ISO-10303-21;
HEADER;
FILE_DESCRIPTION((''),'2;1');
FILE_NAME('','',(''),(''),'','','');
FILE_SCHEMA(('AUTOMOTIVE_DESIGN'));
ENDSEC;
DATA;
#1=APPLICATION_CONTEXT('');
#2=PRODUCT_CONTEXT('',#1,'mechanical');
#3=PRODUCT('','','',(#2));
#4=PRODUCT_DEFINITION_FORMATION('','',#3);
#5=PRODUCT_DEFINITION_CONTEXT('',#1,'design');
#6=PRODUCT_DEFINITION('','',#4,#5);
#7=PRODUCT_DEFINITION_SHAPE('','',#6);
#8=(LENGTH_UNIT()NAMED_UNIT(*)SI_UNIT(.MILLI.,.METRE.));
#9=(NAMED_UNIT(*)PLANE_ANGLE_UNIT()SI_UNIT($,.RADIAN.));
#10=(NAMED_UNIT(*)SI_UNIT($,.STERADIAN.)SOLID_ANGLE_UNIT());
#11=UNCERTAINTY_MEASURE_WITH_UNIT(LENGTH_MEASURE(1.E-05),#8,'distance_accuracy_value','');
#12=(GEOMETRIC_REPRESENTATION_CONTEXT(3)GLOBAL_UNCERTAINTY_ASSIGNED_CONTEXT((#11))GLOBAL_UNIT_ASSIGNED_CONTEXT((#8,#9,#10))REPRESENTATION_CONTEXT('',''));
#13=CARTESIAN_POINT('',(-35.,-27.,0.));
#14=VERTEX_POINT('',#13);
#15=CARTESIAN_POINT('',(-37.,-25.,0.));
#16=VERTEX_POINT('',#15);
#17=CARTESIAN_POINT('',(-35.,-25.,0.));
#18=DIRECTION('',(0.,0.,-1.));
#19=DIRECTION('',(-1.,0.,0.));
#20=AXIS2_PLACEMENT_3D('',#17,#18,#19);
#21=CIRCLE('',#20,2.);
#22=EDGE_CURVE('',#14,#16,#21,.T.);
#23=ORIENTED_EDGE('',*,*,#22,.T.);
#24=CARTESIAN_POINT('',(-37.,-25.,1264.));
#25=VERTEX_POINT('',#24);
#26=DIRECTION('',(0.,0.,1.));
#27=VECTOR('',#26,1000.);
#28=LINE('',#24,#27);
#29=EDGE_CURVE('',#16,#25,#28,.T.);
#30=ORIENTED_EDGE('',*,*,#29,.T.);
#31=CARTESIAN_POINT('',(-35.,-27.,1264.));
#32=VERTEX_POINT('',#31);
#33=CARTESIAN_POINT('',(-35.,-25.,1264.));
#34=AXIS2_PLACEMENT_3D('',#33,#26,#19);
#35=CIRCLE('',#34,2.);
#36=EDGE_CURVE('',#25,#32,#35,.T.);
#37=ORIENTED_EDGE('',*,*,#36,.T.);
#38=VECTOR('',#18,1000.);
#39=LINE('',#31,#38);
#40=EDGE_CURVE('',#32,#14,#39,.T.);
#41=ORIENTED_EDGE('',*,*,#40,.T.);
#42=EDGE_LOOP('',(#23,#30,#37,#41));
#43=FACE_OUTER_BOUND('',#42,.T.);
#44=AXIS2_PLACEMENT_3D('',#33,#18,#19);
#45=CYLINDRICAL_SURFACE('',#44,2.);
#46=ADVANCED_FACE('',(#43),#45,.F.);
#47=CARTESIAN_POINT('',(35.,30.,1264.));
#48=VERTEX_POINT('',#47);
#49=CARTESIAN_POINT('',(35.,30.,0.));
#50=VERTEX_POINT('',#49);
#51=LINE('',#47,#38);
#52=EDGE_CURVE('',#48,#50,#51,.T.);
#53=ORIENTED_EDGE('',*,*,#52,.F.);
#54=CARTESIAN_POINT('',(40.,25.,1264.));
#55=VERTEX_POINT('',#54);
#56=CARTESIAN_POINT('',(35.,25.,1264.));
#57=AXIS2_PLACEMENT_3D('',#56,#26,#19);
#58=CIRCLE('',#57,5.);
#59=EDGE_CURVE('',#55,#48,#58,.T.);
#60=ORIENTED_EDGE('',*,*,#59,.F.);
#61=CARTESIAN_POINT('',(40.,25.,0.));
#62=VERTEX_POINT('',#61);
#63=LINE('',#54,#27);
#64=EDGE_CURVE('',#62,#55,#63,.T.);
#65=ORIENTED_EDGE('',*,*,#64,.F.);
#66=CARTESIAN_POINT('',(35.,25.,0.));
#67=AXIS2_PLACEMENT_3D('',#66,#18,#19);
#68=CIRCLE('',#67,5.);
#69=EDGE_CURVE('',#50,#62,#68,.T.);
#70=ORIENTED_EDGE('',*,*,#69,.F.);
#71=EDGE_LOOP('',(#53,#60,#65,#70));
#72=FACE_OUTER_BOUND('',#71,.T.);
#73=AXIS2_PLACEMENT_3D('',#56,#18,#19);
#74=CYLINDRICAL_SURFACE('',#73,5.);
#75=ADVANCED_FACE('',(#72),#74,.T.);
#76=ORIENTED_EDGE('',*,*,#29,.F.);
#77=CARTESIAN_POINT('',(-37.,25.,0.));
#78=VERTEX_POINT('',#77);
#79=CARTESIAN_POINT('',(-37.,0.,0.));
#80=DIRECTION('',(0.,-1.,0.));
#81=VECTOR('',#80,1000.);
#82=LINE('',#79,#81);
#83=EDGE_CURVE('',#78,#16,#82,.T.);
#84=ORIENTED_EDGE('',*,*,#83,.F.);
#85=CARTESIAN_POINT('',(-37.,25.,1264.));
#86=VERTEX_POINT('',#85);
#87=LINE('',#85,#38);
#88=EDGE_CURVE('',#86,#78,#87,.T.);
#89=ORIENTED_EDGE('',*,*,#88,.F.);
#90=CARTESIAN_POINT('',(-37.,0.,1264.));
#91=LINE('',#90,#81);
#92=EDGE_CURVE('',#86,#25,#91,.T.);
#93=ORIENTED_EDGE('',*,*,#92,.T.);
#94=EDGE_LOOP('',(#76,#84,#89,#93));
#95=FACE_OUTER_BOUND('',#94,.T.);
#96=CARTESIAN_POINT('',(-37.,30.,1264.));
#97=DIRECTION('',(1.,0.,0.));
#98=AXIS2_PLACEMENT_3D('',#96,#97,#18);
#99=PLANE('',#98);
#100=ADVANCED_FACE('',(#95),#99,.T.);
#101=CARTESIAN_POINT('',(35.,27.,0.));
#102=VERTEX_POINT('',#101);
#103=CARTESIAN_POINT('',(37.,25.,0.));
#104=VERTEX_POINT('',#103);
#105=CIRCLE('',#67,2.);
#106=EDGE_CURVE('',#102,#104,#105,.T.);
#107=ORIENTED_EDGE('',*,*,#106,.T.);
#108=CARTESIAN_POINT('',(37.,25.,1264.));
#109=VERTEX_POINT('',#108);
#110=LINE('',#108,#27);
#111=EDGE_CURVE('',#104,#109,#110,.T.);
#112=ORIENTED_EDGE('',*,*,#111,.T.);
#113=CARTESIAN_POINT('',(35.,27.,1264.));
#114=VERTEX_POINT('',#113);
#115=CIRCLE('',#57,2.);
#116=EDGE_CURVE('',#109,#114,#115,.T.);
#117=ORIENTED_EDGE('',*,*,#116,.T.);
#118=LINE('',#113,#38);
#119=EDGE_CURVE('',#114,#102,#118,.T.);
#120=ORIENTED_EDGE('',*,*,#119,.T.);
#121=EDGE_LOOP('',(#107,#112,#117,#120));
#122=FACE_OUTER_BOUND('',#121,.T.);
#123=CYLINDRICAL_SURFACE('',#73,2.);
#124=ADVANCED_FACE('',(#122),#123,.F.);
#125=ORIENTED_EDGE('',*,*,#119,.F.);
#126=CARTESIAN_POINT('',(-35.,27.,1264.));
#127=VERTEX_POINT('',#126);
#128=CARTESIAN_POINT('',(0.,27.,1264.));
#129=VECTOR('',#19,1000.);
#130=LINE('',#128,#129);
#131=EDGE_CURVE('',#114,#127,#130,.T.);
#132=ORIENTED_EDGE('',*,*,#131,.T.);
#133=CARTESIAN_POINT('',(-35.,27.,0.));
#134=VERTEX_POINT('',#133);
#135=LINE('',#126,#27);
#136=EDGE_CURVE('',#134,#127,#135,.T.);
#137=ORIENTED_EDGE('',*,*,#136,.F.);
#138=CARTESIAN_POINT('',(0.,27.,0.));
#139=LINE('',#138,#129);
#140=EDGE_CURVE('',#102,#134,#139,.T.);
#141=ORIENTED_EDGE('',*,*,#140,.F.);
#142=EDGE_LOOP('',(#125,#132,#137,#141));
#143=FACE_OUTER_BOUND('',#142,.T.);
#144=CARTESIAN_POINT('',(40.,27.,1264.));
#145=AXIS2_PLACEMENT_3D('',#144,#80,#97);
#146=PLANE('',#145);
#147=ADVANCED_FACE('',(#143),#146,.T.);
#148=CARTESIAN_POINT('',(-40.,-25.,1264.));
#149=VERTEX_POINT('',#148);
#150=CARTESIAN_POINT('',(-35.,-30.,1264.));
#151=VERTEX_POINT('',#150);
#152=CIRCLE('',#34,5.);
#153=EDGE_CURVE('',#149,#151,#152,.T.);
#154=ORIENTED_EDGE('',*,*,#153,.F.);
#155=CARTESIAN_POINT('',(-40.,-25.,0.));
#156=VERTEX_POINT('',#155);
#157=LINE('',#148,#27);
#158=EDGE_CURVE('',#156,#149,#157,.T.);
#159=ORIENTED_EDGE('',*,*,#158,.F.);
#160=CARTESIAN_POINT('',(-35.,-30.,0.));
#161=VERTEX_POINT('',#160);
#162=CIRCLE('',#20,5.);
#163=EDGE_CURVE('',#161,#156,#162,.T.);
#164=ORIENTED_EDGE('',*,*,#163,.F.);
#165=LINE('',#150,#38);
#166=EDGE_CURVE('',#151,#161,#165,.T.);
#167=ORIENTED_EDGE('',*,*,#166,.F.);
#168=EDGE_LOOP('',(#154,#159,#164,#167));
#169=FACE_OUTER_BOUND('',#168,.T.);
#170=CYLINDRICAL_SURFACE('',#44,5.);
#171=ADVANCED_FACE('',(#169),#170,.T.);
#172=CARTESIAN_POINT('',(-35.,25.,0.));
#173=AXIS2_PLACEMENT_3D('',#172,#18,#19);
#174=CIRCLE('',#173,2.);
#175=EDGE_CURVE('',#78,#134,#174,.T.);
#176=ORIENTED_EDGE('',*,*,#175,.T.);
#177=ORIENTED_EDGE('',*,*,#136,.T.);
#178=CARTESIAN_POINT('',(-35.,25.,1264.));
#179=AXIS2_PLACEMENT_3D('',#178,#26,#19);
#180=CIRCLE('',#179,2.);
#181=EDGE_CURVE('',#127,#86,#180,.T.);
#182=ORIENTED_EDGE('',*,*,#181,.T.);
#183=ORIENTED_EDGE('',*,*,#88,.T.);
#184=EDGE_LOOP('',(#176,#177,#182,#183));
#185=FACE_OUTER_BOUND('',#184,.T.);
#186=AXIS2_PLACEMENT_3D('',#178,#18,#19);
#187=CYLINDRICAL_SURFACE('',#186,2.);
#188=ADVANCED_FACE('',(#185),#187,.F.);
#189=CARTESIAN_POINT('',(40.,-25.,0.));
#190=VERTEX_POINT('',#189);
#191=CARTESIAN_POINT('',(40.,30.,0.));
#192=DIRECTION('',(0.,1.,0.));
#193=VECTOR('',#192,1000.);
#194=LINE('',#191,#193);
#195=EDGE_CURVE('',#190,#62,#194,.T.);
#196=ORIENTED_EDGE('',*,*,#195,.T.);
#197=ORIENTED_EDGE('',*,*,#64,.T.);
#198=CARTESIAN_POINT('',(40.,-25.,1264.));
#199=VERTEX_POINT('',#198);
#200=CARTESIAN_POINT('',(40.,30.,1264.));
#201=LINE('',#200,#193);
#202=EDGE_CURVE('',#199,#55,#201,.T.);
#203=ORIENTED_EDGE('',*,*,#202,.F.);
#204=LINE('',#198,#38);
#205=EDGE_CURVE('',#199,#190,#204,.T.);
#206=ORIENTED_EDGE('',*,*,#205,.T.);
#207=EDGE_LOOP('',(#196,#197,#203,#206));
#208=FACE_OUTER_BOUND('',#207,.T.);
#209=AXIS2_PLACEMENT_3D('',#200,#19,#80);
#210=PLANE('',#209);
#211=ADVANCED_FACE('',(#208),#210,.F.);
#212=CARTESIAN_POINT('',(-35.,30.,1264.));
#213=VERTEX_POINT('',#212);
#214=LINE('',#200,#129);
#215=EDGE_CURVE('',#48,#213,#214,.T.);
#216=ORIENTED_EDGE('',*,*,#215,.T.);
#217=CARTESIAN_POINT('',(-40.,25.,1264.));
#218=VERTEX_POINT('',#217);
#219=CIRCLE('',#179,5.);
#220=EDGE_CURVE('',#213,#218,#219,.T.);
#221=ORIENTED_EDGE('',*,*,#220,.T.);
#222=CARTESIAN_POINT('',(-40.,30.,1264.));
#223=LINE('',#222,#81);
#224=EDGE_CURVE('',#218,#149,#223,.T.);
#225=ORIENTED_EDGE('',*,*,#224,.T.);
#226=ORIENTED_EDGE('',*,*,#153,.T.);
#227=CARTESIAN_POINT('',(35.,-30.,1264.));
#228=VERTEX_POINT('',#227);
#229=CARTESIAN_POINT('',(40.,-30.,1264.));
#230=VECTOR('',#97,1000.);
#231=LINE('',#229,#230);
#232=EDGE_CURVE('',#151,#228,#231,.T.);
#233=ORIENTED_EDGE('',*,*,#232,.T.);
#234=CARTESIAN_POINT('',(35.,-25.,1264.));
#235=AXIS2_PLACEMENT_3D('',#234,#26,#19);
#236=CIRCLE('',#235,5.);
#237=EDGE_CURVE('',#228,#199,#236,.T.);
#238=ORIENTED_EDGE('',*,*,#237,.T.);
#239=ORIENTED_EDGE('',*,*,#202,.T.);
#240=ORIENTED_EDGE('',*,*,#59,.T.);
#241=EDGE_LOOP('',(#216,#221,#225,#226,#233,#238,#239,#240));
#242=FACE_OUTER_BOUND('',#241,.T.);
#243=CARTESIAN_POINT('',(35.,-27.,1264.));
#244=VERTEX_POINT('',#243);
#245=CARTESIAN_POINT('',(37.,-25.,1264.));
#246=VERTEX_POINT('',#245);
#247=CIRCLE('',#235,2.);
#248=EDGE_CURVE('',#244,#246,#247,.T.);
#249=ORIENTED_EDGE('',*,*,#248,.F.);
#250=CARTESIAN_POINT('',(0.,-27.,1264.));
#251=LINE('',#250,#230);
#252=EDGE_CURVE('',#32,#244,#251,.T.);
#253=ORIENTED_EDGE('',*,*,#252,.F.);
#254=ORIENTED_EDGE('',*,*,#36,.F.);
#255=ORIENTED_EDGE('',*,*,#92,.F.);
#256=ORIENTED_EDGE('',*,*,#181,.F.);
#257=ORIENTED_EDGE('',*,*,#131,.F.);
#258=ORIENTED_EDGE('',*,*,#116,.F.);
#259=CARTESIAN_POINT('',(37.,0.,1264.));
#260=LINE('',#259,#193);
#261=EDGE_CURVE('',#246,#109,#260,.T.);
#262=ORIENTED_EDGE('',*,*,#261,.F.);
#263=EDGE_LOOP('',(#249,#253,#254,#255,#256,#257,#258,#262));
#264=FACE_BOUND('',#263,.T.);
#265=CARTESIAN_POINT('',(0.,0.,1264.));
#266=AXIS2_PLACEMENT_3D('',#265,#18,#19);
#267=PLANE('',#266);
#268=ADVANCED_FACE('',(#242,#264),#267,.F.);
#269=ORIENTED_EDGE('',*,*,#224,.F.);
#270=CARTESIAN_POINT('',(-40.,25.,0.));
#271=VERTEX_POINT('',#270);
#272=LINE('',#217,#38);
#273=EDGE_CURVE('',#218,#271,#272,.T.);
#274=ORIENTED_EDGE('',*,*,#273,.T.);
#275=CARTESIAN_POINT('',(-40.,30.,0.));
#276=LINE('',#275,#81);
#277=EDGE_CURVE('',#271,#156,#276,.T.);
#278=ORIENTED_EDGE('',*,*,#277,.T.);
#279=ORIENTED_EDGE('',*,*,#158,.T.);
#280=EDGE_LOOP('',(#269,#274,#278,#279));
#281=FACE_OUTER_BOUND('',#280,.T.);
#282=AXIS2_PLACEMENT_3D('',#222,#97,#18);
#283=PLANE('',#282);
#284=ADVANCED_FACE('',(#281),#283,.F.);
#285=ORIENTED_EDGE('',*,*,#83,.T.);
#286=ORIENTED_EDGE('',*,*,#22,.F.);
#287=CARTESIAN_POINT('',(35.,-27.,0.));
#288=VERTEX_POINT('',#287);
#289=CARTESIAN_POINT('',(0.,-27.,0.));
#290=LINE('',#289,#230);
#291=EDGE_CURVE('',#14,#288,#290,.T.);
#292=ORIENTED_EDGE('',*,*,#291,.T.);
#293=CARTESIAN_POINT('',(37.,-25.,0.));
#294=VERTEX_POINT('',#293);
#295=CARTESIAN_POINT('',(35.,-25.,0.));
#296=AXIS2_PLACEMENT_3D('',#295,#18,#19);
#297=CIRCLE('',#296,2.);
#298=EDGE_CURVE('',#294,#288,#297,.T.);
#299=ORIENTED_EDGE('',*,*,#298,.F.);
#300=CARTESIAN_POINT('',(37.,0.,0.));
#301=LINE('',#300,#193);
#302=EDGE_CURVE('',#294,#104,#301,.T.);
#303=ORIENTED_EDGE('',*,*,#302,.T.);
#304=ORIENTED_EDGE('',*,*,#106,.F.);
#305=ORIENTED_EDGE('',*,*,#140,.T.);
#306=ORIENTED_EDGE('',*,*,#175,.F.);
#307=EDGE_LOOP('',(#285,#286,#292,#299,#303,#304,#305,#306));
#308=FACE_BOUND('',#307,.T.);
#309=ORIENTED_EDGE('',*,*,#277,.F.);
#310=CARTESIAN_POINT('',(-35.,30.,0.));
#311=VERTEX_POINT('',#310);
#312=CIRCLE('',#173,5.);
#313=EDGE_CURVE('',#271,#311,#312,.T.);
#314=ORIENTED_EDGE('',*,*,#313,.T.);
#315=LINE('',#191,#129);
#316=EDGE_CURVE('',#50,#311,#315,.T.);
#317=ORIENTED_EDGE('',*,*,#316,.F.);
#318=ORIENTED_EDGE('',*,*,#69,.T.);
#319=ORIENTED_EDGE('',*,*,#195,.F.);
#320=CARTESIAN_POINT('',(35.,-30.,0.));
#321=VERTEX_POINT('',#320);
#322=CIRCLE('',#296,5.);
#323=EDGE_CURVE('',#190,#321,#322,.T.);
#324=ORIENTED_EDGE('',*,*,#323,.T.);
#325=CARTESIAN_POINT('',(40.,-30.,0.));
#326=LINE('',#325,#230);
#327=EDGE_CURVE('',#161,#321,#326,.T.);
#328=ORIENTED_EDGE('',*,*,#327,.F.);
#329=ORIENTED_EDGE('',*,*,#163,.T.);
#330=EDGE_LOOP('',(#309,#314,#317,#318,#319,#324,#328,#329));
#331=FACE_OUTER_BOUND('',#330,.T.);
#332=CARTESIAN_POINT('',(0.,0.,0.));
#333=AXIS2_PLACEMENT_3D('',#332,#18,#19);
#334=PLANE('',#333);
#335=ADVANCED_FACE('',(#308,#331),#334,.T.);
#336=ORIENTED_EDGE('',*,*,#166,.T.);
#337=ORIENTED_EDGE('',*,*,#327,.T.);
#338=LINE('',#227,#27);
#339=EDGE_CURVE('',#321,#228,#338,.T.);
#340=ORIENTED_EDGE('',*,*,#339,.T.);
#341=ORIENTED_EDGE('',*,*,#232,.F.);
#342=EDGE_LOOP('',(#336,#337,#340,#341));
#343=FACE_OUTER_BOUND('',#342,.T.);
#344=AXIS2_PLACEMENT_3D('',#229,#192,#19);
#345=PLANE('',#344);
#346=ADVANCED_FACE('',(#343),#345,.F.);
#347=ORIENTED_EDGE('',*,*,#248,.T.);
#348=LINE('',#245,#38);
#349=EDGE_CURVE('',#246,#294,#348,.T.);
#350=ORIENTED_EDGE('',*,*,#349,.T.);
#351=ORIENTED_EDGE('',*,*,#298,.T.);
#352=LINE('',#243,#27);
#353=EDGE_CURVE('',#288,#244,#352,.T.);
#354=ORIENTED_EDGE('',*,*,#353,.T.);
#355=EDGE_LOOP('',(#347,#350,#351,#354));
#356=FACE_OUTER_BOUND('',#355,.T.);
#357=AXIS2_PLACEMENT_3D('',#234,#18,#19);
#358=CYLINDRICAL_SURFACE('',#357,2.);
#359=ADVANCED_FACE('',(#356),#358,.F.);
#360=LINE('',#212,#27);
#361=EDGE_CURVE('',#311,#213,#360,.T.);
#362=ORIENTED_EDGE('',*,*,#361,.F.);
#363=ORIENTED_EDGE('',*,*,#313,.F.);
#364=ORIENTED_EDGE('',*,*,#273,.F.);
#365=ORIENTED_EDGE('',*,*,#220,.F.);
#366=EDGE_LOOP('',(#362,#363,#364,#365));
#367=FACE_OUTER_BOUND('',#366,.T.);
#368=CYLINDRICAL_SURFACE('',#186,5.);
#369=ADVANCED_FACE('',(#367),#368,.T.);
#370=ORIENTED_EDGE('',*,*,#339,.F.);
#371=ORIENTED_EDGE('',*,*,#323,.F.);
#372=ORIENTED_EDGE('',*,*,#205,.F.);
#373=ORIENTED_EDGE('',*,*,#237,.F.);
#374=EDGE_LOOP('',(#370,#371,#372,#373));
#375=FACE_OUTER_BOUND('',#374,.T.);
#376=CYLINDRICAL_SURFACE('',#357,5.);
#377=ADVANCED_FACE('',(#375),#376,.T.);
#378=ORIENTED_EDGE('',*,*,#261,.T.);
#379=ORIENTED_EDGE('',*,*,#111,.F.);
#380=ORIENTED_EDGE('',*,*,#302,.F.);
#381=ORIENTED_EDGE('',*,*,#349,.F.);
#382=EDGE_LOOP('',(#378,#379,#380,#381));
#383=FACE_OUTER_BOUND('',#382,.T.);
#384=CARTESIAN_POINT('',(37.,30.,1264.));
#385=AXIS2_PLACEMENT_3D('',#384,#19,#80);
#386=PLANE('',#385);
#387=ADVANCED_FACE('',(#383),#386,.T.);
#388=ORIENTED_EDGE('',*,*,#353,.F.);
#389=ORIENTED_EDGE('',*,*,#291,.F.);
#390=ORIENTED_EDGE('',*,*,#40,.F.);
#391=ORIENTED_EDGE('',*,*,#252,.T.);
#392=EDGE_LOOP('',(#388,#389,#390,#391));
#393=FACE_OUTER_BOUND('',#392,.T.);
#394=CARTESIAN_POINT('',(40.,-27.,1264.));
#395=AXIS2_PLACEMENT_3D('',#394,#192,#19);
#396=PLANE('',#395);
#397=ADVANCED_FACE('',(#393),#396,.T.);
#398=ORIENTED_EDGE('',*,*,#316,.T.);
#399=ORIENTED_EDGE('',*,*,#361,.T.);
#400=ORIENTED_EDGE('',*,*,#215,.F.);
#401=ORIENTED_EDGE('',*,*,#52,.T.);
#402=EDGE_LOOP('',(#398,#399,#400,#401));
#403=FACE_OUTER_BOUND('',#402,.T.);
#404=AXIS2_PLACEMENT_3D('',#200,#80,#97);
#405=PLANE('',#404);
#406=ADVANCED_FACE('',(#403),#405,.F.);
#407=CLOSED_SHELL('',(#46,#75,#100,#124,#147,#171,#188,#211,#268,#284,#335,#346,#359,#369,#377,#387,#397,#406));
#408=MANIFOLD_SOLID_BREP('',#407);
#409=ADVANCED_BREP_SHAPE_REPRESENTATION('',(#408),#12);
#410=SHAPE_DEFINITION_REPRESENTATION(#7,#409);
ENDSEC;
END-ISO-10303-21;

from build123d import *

# Parameters (mm, degrees)
SKETCH_1_W      = 80
SKETCH_1_H      = 60
EXTRUDE_1_DEPTH = 1264
FILLET_1_R      = 5
SHELL_1_T       = -3


with BuildPart() as part:
    # 草图1 → 凸台-拉伸1 (new body)
    with BuildSketch(Plane.XY):
        Rectangle(SKETCH_1_W, SKETCH_1_H)
    extrude(amount=EXTRUDE_1_DEPTH)

    # 圆角1
    fillet_1_edges = [part.edges().sort_by_distance(p)[0] for p in [
        (-40, 30, 632),
        (40, 30, 632),
        (40, -30, 632),
        (-40, -30, 632),
    ]]
    fillet(fillet_1_edges, radius=FILLET_1_R)

    # 抽壳1
    shell_1_openings = [part.faces().sort_by_distance(p)[0] for p in [
        (0, 0, 1264),
        (0, 0, 0),
    ]]
    offset(amount=SHELL_1_T, openings=shell_1_openings, kind=Kind.INTERSECTION)


solid = part.part
